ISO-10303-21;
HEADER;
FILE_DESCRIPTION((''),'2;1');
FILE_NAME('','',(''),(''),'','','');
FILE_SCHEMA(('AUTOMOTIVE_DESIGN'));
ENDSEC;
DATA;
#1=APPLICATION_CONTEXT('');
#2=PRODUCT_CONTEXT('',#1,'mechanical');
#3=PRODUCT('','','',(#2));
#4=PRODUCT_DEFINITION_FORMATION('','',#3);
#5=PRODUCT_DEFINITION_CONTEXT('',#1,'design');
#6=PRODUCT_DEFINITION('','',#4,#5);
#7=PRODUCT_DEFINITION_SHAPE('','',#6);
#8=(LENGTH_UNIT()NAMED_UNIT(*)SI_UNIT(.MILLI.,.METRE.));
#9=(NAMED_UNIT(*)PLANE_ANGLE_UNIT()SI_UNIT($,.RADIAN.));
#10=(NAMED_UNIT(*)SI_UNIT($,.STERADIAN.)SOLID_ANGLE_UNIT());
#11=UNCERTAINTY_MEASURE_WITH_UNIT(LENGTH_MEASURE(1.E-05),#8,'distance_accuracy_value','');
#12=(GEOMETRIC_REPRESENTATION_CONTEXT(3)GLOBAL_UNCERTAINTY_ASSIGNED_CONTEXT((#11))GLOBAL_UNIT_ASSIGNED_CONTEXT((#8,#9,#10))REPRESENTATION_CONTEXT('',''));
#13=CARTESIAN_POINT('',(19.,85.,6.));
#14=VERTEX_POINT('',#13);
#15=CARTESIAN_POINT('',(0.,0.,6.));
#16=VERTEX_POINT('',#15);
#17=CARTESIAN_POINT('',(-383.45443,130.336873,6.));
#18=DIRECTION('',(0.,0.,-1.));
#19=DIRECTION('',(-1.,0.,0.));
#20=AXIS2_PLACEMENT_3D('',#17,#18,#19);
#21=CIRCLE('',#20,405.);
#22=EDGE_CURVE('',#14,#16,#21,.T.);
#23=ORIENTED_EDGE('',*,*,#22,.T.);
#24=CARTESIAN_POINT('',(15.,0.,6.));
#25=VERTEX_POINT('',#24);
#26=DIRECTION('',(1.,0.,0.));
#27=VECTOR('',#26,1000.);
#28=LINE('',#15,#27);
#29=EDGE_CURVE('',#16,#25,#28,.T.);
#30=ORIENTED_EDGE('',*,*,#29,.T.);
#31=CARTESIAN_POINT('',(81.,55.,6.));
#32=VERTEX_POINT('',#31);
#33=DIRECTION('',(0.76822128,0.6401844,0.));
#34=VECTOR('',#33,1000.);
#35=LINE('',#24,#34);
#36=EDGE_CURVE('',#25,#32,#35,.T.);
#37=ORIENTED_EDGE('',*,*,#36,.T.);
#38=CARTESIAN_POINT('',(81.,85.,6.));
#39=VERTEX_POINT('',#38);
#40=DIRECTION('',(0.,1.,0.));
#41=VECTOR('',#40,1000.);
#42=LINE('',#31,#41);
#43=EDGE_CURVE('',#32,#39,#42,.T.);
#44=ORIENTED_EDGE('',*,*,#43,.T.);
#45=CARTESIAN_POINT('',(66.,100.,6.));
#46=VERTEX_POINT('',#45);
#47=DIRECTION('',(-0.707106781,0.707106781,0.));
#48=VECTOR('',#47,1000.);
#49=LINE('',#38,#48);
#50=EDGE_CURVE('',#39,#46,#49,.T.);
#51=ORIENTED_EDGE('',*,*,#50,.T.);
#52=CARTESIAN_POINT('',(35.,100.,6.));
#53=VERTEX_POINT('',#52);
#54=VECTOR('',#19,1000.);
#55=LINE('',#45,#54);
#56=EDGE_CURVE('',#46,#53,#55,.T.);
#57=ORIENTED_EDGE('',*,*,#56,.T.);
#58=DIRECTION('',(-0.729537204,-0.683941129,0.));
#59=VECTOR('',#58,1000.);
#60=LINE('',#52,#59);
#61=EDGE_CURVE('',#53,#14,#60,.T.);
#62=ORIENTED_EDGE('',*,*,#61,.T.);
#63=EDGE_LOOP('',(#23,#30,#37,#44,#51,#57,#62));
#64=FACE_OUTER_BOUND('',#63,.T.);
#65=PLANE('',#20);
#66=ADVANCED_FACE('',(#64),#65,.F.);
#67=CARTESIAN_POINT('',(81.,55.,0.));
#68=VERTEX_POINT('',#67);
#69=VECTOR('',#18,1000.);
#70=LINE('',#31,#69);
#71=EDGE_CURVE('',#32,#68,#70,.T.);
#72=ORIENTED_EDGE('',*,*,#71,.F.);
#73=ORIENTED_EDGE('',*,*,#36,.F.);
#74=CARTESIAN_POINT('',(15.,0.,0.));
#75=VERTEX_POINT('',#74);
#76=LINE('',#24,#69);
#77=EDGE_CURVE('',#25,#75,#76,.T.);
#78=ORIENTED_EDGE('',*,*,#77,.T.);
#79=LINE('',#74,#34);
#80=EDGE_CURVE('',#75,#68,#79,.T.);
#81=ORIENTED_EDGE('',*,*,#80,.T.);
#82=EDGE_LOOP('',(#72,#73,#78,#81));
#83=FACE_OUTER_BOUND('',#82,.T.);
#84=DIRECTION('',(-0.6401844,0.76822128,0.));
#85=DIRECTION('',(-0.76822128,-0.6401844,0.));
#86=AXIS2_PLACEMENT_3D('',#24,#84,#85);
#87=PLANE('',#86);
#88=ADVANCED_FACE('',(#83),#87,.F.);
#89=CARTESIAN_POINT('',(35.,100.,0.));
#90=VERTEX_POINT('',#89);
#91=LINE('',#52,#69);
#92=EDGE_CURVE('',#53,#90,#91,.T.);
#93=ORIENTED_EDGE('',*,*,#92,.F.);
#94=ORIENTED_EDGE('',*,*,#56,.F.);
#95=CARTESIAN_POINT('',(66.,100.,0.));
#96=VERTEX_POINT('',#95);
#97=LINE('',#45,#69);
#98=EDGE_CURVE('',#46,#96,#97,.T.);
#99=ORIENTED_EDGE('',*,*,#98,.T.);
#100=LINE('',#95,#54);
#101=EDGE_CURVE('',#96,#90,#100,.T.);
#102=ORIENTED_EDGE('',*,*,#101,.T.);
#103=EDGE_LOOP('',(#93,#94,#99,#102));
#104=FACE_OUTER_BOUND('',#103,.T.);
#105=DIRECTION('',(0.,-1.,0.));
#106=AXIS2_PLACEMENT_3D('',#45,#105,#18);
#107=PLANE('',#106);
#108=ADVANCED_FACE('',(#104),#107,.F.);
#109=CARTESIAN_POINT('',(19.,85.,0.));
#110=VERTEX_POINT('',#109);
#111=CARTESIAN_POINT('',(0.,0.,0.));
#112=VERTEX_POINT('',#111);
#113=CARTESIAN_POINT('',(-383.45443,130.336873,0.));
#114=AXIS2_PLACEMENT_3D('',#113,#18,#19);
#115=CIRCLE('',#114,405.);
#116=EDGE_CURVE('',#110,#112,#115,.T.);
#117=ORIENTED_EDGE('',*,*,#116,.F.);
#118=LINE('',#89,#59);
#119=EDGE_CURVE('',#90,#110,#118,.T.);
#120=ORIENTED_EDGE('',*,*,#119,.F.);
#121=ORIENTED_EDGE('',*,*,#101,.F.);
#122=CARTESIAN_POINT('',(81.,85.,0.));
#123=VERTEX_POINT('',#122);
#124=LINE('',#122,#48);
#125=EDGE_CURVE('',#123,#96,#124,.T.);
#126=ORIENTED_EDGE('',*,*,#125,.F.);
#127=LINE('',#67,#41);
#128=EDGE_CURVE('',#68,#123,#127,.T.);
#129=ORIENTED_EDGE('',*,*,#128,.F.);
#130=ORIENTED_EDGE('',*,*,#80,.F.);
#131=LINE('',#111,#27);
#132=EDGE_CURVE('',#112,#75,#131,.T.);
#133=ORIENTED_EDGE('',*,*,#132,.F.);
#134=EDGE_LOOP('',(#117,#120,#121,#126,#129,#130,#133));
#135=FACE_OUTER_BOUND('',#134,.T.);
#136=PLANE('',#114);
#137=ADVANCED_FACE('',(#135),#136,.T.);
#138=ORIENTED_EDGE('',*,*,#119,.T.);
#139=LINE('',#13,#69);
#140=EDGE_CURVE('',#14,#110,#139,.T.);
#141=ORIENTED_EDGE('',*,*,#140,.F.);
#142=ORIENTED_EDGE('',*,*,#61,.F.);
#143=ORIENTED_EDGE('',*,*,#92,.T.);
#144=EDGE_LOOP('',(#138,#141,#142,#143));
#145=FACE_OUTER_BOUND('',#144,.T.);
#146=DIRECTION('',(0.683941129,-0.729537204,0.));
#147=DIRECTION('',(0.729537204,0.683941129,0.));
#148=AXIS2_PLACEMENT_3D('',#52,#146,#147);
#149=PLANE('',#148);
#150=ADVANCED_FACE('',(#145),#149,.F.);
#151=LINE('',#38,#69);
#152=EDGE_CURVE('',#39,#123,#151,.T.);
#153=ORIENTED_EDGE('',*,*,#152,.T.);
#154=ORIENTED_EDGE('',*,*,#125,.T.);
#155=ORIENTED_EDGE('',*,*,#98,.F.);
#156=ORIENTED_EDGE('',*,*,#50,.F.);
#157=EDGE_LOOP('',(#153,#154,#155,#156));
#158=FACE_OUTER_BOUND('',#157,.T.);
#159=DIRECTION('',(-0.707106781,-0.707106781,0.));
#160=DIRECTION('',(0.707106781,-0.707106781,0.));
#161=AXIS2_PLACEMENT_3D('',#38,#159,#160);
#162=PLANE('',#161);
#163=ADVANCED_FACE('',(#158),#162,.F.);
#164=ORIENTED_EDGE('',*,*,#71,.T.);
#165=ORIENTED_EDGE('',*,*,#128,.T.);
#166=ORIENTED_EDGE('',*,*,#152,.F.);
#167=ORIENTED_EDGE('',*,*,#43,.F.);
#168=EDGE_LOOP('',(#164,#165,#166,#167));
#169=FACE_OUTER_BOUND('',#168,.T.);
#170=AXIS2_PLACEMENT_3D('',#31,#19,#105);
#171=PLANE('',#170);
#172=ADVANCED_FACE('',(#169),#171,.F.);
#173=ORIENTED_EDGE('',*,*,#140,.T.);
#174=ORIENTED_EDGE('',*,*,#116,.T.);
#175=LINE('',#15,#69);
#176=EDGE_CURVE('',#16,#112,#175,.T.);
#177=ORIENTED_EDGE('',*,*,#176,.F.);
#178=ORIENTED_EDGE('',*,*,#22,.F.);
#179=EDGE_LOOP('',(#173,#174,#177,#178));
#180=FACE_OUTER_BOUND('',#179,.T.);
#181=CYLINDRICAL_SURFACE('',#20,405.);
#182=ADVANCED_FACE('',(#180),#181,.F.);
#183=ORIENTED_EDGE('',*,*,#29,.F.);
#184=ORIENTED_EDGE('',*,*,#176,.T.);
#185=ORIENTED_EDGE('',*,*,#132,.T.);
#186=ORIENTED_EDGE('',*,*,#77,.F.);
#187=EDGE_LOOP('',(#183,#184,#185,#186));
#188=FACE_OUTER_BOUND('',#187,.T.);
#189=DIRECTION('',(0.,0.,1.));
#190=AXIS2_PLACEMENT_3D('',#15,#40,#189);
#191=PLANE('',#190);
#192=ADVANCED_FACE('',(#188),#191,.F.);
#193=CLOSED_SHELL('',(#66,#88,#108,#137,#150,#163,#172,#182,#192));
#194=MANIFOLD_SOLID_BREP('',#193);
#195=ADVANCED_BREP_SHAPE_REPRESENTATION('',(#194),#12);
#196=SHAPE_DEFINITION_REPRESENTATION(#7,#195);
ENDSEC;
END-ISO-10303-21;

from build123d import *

# Parameters (mm, degrees)
BOSS_EXTRUDE1_DEPTH = 6


with BuildPart() as part:
    # Sketch1 → Boss-Extrude1 (new body)
    with BuildSketch(Plane.XY):
        with BuildLine():
            Line((0, 0), (15, 0))
            Line((15, 0), (81, 55))
            Line((81, 55), (81, 85))
            Line((81, 85), (66, 100))
            Line((66, 100), (35, 100))
            Line((35, 100), (19, 85))
            ThreePointArc((19, 85), (11.791612432, 41.987757221), (0, 0))
        make_face()
    extrude(amount=BOSS_EXTRUDE1_DEPTH)


solid = part.part
